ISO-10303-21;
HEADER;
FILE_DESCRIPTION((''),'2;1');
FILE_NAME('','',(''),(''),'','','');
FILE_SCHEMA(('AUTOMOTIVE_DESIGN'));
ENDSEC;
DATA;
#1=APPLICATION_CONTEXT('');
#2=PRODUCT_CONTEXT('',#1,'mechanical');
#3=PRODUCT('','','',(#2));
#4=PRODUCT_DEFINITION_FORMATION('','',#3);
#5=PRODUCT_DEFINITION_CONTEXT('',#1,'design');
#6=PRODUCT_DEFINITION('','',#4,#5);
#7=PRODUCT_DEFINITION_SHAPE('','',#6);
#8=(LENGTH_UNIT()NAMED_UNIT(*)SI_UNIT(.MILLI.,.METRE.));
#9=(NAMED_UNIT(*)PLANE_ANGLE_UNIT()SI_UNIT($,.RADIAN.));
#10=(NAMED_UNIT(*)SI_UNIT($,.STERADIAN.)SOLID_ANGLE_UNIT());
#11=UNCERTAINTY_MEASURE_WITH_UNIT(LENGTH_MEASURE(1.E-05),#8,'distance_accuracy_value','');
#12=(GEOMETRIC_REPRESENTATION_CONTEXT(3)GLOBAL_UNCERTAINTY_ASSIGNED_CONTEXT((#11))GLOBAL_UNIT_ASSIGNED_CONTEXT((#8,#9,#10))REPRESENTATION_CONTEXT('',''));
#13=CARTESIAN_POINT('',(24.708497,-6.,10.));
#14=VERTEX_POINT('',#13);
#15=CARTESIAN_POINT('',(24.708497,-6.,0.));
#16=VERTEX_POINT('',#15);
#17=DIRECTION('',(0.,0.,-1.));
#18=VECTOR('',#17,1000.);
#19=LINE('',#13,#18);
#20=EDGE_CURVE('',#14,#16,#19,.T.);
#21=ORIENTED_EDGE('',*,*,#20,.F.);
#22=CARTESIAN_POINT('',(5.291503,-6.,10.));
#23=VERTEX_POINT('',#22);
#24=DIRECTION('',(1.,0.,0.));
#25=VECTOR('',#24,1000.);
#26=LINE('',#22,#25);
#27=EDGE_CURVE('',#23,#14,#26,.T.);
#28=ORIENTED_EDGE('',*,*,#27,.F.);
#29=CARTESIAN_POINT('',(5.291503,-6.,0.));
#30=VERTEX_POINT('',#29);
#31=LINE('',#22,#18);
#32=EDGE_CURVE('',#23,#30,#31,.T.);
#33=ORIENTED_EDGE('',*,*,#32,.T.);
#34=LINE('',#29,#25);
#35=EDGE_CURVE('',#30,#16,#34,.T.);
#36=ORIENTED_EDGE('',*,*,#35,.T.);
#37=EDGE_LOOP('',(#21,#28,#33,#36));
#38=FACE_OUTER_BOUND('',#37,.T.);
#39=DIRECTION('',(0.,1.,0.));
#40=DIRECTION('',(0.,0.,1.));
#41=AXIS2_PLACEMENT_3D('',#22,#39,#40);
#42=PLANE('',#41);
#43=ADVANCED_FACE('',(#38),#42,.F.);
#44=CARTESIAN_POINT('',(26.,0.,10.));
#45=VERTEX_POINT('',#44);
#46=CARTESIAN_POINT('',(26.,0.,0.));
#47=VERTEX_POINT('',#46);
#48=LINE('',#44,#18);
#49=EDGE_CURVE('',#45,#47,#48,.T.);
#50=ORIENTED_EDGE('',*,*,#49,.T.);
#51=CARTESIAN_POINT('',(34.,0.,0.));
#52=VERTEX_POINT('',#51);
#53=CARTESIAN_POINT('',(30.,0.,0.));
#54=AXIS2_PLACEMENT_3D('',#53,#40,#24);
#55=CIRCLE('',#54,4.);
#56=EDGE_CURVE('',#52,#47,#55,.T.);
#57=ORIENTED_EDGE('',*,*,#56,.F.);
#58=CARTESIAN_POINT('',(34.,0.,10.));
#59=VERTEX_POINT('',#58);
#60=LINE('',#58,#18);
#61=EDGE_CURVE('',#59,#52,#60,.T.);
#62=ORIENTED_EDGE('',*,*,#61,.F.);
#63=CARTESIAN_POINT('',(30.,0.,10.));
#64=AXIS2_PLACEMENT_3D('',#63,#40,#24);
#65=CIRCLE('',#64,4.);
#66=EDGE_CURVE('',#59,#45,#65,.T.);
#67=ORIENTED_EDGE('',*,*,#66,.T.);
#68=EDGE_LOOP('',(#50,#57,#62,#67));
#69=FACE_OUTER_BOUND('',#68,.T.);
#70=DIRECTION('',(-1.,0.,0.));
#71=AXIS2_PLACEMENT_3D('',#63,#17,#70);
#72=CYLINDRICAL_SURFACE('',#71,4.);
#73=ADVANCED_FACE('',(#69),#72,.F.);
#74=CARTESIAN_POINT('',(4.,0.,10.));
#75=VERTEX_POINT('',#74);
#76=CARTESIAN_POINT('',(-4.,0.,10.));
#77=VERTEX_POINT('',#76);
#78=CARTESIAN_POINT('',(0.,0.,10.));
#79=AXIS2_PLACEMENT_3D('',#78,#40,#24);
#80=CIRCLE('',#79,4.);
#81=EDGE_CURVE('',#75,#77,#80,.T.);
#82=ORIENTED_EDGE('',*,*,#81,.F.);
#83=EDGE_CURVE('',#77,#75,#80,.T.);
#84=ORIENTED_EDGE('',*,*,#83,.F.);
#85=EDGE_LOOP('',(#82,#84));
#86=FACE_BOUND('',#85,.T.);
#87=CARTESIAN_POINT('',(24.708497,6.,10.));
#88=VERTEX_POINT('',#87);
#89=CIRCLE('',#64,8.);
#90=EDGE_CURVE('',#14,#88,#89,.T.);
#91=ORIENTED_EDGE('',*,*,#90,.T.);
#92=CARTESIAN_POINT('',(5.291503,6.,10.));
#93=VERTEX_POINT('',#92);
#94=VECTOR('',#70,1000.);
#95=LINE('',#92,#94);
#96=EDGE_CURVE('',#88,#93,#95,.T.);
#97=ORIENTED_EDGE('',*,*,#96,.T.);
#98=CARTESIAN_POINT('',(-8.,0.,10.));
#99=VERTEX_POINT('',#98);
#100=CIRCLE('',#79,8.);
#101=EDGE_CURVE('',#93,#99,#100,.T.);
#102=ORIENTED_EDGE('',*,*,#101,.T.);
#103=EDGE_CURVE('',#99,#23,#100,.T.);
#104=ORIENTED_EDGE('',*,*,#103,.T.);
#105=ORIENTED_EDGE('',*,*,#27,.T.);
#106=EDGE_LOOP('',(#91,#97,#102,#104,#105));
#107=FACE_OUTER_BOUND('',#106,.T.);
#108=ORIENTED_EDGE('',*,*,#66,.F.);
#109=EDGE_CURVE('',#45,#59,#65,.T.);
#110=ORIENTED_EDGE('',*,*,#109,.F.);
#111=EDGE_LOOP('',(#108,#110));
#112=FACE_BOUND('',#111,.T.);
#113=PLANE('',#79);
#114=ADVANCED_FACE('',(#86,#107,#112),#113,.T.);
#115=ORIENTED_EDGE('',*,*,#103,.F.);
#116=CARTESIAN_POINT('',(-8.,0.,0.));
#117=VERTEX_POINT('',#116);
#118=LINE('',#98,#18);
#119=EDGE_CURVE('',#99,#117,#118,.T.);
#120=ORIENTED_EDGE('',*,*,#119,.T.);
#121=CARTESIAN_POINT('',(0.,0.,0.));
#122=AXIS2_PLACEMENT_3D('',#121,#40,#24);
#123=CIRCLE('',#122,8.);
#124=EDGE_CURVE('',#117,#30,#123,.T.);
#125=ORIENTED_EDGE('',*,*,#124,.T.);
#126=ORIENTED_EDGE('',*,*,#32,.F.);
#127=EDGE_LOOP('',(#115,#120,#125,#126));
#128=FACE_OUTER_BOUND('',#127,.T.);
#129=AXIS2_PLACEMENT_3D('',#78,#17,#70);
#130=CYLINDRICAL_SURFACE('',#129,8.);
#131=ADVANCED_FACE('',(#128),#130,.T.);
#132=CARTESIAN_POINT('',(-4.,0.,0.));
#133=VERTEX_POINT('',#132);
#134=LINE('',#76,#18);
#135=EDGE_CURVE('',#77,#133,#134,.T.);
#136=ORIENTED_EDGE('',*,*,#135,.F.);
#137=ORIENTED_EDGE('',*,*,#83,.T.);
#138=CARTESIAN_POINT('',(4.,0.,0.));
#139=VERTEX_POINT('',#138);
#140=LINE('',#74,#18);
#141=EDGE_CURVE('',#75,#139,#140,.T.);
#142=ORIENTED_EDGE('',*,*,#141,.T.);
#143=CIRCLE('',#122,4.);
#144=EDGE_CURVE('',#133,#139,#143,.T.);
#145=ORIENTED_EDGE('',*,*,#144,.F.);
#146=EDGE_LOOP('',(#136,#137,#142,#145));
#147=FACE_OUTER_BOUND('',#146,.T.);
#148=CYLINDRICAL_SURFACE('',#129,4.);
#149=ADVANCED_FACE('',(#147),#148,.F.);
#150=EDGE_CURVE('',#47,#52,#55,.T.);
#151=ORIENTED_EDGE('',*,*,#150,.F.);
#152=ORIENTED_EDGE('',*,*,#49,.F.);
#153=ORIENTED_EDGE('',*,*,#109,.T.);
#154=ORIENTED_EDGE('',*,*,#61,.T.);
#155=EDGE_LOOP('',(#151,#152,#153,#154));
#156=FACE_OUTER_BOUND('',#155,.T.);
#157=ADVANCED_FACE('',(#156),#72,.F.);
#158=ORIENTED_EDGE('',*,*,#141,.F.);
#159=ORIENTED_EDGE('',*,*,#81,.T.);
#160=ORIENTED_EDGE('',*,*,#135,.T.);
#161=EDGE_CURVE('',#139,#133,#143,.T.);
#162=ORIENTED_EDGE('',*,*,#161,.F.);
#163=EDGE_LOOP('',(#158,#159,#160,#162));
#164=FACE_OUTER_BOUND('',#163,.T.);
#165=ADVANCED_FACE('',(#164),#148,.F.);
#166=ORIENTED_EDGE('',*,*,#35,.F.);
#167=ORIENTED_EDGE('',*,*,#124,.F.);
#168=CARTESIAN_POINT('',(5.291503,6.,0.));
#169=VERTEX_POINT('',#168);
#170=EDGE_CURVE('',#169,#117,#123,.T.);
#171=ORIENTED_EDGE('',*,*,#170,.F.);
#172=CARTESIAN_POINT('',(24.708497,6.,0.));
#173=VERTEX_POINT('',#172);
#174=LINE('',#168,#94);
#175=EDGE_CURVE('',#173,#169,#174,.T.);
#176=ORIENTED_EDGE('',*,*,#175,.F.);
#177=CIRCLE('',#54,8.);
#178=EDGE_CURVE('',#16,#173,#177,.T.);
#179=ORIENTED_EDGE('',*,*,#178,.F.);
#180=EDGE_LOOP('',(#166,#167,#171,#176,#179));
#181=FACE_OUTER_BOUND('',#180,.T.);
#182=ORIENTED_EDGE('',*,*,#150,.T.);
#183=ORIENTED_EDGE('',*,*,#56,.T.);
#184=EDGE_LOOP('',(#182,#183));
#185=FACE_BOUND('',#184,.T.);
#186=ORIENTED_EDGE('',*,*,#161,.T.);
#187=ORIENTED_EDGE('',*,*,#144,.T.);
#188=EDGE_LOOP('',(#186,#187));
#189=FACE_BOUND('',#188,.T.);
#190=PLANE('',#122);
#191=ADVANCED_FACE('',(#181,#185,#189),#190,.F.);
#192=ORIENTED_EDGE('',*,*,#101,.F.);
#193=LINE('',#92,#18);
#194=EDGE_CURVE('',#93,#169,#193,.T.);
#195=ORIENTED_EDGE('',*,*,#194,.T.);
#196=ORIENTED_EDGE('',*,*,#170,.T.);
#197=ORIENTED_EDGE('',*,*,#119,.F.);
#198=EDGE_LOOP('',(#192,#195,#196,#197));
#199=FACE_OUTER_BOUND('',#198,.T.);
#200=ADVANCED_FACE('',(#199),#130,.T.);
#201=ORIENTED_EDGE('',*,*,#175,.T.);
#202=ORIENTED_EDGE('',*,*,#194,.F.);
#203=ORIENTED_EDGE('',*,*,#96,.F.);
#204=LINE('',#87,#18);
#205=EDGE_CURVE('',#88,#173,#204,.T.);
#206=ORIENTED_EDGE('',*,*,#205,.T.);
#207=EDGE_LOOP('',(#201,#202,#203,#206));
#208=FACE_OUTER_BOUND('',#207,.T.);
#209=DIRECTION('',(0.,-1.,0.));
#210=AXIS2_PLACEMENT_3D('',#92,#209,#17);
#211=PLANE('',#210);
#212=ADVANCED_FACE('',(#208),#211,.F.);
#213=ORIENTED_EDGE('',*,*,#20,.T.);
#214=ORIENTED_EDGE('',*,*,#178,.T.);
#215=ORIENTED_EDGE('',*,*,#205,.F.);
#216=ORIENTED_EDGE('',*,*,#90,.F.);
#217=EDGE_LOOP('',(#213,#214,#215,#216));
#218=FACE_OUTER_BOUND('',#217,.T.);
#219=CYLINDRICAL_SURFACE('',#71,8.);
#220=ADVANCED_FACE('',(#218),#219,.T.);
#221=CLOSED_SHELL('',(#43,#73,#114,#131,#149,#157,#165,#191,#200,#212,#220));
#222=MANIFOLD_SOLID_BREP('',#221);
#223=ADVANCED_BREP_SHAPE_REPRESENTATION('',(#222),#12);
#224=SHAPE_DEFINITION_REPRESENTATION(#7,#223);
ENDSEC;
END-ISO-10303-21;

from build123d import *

# Parameters (mm, degrees)
SKETCH1_R           = 4
BOSS_EXTRUDE1_DEPTH = 10


with BuildPart() as part:
    # Sketch1 → Boss-Extrude1 (new body)
    with BuildSketch(Plane.XY):
        with BuildLine():
            Line((5.291502622, -6), (24.708497378, -6))
            ThreePointArc((24.708497378, -6), (38, 0), (24.708497378, 6))
            Line((24.708497378, 6), (5.291502622, 6))
            ThreePointArc((5.291502622, 6), (-8, 0), (5.291502622, -6))
        make_face()
        Circle(SKETCH1_R, mode=Mode.SUBTRACT)
        with Locations((30, 0)):
            Circle(SKETCH1_R, mode=Mode.SUBTRACT)
    extrude(amount=BOSS_EXTRUDE1_DEPTH)


solid = part.part
